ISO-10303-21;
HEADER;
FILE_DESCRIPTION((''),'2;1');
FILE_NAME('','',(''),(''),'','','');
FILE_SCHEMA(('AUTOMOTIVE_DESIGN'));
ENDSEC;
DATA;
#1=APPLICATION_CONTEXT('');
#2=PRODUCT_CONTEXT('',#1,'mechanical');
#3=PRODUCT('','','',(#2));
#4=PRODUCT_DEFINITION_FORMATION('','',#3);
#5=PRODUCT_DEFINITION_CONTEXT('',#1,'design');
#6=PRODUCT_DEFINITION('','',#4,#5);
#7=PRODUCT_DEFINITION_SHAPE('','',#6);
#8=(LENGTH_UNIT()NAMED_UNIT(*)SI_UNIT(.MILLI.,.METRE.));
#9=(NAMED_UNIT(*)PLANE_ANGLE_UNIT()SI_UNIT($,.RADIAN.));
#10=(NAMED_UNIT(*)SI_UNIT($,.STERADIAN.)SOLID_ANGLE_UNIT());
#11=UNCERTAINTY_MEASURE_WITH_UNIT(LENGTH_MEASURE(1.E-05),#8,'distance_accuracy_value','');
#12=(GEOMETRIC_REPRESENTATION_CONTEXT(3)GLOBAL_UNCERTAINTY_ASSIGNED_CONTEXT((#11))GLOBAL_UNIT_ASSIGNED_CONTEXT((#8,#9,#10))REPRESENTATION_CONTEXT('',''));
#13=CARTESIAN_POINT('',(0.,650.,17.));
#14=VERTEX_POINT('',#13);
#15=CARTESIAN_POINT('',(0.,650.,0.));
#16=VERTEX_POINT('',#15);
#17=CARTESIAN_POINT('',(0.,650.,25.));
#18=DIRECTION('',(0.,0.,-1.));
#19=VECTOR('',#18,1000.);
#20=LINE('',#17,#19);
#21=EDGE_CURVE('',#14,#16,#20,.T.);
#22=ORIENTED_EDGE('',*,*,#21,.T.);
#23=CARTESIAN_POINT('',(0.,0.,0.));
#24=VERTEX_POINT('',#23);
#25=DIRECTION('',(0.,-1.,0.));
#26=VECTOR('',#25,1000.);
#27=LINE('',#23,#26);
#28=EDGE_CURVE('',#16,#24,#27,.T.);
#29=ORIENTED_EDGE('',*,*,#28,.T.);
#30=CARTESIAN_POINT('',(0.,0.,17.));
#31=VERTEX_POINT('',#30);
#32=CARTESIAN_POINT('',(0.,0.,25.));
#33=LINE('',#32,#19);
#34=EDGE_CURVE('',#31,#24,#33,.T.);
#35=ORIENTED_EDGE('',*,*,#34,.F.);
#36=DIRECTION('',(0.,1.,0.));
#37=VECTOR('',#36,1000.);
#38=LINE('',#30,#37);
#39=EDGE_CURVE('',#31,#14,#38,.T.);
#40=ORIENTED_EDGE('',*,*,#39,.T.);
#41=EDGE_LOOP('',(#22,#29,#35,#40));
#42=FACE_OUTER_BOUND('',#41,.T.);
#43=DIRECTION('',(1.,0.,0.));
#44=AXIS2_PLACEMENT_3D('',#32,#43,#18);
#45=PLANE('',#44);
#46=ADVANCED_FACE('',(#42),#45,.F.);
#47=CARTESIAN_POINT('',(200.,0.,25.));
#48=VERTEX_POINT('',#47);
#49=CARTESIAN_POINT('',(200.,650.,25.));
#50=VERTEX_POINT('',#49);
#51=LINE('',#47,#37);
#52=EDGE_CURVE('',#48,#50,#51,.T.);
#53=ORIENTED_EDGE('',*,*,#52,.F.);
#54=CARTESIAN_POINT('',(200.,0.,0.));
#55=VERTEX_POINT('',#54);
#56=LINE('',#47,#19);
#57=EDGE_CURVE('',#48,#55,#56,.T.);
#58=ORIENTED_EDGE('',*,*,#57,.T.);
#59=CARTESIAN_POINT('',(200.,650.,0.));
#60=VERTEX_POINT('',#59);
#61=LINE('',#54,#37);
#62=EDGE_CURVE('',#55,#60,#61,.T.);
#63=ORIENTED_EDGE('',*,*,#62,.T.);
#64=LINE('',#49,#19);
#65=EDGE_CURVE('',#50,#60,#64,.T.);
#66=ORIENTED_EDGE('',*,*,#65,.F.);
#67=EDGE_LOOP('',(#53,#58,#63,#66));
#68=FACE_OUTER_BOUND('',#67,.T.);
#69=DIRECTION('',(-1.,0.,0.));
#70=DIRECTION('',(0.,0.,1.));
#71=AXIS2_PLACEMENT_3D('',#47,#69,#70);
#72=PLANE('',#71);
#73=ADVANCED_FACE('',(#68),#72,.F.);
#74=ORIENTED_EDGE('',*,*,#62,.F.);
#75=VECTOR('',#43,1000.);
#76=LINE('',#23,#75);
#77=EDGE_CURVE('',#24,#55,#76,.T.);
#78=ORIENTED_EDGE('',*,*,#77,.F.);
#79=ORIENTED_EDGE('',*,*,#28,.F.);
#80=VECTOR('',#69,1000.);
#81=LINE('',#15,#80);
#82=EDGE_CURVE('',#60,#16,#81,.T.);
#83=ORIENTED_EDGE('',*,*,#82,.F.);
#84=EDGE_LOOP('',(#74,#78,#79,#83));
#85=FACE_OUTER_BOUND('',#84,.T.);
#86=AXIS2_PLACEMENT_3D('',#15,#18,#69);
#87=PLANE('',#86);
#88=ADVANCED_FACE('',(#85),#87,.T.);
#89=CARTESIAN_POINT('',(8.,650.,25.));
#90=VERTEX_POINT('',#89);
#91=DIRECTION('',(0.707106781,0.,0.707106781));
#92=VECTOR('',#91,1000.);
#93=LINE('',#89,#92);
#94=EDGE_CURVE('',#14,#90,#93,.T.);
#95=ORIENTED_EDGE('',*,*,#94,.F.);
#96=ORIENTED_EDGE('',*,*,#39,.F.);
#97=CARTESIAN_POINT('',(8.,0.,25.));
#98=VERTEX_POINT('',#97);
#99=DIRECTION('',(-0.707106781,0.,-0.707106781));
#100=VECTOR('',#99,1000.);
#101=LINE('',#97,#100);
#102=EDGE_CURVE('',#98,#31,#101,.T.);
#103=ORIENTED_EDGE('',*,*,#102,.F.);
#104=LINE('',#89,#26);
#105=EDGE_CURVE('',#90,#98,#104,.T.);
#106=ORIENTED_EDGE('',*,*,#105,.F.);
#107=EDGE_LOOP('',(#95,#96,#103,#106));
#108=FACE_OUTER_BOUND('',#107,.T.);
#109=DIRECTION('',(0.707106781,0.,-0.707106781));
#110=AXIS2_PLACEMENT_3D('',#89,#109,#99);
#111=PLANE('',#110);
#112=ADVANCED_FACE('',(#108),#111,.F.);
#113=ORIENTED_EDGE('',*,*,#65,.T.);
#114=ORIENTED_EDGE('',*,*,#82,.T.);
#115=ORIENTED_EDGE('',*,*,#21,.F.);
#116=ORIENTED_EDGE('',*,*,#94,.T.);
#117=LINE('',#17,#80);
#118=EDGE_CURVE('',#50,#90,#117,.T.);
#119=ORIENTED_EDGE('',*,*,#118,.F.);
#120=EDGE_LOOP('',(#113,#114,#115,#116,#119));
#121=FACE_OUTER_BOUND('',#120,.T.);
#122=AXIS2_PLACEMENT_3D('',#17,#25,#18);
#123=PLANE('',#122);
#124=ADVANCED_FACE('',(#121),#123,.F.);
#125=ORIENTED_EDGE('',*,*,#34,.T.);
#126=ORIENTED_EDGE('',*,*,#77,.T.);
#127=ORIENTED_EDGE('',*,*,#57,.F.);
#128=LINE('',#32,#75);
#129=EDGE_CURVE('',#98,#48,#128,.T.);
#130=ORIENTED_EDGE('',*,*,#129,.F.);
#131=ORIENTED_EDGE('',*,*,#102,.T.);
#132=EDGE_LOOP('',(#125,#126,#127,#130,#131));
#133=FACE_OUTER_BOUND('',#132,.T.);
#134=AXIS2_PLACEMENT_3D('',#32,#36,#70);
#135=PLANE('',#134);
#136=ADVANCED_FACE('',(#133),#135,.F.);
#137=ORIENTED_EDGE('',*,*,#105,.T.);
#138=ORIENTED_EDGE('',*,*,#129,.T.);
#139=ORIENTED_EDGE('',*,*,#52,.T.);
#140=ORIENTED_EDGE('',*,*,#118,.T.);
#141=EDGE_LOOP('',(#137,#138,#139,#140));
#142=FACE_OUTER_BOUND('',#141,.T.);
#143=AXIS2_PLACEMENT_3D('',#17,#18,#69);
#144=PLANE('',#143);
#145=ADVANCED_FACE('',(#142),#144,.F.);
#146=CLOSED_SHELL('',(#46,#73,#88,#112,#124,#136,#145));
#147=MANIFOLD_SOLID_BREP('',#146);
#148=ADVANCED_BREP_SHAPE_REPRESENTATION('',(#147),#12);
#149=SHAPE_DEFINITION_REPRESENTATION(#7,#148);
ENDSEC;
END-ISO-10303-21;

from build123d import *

# Parameters (mm, degrees)
SKETCH1_W           = 200
SKETCH1_H           = 650
BOSS_EXTRUDE1_DEPTH = 25
CHAMFER1_SIZE       = 8


with BuildPart() as part:
    # Sketch1 → Boss-Extrude1 (new body)
    with BuildSketch(Plane.XY):
        with Locations((100, 325)):
            Rectangle(SKETCH1_W, SKETCH1_H)
    extrude(amount=BOSS_EXTRUDE1_DEPTH)

    # Chamfer1
    chamfer1_edges = [part.edges().sort_by_distance(p)[0] for p in [
        (0, 325, 25),
    ]]
    chamfer(chamfer1_edges, length=CHAMFER1_SIZE)


solid = part.part
